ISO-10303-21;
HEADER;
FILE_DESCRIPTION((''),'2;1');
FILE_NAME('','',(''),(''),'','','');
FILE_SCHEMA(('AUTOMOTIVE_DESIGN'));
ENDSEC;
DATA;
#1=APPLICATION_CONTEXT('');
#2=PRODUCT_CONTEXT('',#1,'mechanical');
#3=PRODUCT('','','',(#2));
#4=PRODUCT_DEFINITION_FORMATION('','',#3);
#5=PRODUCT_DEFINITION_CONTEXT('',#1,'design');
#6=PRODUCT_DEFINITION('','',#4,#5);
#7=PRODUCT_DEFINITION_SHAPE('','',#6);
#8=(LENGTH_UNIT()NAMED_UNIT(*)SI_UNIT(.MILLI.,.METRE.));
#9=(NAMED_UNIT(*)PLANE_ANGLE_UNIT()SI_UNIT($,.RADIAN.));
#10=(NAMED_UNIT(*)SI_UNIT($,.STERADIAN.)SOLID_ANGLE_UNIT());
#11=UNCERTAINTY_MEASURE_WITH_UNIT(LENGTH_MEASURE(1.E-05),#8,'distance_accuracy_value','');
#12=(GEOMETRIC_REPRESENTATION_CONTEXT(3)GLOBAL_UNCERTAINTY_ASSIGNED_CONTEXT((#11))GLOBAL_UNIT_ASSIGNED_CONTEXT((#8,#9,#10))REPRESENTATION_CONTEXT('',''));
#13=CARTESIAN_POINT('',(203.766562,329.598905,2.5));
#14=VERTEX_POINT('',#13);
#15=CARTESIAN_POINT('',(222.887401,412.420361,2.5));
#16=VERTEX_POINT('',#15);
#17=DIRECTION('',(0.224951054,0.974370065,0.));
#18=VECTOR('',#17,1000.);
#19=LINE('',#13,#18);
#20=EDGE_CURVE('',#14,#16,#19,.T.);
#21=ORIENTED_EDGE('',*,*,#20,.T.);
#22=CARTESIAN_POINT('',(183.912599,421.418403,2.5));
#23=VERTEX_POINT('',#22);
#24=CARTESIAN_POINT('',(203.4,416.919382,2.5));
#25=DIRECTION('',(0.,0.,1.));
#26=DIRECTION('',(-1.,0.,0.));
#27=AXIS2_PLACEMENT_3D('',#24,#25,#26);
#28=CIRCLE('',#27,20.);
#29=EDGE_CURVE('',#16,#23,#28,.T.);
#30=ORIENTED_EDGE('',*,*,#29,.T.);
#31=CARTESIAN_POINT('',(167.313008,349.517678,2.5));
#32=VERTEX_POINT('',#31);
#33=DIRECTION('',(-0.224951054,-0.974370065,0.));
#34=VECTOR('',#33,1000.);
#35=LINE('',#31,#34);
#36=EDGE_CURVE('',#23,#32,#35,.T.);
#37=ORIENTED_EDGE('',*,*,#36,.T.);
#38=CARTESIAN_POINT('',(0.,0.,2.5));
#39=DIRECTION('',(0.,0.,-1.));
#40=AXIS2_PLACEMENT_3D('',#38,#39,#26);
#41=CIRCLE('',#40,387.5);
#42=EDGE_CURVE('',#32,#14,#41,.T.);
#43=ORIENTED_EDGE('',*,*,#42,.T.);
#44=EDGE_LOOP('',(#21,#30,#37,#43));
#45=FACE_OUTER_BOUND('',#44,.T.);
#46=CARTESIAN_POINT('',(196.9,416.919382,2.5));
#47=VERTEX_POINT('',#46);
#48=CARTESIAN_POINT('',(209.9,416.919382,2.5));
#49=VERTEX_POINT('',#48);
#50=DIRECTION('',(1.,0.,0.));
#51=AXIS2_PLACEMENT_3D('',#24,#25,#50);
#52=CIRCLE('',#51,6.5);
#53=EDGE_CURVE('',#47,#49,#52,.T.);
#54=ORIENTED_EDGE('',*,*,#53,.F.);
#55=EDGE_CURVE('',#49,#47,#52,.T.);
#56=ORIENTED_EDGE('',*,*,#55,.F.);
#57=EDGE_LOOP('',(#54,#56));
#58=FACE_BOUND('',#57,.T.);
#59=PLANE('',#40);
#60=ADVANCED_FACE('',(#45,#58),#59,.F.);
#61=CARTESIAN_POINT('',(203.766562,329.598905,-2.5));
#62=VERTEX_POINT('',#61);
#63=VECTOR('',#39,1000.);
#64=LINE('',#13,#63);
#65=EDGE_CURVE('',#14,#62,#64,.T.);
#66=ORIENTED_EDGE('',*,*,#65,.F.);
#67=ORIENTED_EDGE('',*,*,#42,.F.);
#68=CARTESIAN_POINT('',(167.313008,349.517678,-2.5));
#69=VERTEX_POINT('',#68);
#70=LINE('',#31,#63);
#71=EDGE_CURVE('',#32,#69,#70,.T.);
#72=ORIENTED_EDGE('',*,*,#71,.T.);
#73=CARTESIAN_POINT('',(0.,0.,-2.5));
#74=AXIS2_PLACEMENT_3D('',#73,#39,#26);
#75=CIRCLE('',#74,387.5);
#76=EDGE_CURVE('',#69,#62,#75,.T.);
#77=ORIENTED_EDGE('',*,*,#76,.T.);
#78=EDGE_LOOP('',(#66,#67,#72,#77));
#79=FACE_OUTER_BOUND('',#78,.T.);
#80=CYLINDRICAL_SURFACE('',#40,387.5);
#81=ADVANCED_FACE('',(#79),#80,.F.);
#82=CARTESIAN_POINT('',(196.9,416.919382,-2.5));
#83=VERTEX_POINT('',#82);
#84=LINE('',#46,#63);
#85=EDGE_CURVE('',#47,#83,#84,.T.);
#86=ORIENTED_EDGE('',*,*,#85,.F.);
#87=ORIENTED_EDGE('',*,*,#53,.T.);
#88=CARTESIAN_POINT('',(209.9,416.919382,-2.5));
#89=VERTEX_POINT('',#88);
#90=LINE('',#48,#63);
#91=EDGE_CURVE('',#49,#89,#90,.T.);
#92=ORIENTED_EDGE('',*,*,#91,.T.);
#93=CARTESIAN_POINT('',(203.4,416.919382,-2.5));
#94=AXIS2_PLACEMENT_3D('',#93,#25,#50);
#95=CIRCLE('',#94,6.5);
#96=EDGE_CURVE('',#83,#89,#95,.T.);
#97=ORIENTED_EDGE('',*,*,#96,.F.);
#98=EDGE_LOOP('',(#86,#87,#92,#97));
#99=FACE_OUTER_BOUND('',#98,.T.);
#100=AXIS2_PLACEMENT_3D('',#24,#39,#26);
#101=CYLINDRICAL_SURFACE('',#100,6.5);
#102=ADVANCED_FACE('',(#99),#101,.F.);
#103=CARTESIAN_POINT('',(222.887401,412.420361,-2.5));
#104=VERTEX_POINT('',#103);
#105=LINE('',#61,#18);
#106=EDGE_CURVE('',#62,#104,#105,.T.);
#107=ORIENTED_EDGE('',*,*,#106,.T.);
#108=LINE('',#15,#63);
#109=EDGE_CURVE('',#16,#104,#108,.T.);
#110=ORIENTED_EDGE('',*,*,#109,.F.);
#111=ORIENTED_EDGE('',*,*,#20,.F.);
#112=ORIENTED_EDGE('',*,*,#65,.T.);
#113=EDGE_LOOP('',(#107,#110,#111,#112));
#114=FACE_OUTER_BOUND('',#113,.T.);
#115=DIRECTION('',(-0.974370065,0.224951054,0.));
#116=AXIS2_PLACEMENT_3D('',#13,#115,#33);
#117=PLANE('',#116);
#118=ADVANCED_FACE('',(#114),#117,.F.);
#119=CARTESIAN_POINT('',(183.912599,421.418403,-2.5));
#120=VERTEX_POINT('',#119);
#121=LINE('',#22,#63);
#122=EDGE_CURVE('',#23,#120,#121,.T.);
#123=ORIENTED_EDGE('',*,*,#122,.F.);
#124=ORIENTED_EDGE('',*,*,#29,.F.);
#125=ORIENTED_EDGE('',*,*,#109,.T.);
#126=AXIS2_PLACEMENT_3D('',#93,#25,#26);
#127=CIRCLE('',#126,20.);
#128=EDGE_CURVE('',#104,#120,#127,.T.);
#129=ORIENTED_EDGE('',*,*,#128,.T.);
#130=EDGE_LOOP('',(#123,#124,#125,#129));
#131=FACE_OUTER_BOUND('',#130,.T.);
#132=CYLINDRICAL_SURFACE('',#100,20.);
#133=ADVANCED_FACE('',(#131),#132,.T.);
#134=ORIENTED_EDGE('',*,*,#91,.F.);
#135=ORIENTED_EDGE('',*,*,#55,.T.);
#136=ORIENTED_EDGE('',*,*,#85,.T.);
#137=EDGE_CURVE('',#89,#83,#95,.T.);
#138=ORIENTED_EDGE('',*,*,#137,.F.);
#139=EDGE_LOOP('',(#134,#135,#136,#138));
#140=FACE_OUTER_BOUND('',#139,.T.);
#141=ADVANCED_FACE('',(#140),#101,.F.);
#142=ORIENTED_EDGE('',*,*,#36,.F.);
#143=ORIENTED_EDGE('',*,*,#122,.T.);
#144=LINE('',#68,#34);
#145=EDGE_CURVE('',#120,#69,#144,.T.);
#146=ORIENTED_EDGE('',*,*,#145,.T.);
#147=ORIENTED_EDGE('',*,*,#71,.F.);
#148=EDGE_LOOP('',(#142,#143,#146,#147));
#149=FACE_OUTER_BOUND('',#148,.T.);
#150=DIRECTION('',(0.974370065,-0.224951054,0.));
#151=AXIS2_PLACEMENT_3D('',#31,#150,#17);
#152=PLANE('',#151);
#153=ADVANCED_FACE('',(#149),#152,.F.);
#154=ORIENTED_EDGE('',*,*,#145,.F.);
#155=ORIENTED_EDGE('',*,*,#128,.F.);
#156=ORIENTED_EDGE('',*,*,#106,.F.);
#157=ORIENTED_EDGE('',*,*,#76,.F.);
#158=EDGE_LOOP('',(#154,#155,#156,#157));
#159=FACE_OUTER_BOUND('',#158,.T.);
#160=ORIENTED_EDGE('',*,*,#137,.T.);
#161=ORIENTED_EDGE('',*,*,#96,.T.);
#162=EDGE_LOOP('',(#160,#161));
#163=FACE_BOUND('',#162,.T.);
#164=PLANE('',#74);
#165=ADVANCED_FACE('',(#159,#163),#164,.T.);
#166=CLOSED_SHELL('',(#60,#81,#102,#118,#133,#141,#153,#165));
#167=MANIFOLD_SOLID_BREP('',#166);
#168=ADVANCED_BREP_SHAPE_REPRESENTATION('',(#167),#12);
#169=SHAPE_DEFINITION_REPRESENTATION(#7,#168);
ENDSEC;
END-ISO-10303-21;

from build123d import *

# Parameters (mm, degrees)
SKETCH1_R           = 6.5
BOSS_EXTRUDE1_DEPTH = 2.5


with BuildPart() as part:
    # Sketch1 → Boss-Extrude1 (new, symmetric)
    with BuildSketch(Plane.XY):
        with BuildLine():
            Line((167.313008395, 349.517677982), (183.912598704, 421.418402931))
            ThreePointArc((183.912598704, 421.418402931), (207.899021087, 436.40678314), (222.887401296, 412.420360758))
            Line((222.887401296, 412.420360758), (203.766561676, 329.598905251))
            ThreePointArc((203.766561676, 329.598905251), (185.806892251, 340.047127311), (167.313008395, 349.517677982))
        make_face()
        with Locations((203.4, 416.919381844)):
            Circle(SKETCH1_R, mode=Mode.SUBTRACT)
    extrude(amount=BOSS_EXTRUDE1_DEPTH, both=True)


solid = part.part
